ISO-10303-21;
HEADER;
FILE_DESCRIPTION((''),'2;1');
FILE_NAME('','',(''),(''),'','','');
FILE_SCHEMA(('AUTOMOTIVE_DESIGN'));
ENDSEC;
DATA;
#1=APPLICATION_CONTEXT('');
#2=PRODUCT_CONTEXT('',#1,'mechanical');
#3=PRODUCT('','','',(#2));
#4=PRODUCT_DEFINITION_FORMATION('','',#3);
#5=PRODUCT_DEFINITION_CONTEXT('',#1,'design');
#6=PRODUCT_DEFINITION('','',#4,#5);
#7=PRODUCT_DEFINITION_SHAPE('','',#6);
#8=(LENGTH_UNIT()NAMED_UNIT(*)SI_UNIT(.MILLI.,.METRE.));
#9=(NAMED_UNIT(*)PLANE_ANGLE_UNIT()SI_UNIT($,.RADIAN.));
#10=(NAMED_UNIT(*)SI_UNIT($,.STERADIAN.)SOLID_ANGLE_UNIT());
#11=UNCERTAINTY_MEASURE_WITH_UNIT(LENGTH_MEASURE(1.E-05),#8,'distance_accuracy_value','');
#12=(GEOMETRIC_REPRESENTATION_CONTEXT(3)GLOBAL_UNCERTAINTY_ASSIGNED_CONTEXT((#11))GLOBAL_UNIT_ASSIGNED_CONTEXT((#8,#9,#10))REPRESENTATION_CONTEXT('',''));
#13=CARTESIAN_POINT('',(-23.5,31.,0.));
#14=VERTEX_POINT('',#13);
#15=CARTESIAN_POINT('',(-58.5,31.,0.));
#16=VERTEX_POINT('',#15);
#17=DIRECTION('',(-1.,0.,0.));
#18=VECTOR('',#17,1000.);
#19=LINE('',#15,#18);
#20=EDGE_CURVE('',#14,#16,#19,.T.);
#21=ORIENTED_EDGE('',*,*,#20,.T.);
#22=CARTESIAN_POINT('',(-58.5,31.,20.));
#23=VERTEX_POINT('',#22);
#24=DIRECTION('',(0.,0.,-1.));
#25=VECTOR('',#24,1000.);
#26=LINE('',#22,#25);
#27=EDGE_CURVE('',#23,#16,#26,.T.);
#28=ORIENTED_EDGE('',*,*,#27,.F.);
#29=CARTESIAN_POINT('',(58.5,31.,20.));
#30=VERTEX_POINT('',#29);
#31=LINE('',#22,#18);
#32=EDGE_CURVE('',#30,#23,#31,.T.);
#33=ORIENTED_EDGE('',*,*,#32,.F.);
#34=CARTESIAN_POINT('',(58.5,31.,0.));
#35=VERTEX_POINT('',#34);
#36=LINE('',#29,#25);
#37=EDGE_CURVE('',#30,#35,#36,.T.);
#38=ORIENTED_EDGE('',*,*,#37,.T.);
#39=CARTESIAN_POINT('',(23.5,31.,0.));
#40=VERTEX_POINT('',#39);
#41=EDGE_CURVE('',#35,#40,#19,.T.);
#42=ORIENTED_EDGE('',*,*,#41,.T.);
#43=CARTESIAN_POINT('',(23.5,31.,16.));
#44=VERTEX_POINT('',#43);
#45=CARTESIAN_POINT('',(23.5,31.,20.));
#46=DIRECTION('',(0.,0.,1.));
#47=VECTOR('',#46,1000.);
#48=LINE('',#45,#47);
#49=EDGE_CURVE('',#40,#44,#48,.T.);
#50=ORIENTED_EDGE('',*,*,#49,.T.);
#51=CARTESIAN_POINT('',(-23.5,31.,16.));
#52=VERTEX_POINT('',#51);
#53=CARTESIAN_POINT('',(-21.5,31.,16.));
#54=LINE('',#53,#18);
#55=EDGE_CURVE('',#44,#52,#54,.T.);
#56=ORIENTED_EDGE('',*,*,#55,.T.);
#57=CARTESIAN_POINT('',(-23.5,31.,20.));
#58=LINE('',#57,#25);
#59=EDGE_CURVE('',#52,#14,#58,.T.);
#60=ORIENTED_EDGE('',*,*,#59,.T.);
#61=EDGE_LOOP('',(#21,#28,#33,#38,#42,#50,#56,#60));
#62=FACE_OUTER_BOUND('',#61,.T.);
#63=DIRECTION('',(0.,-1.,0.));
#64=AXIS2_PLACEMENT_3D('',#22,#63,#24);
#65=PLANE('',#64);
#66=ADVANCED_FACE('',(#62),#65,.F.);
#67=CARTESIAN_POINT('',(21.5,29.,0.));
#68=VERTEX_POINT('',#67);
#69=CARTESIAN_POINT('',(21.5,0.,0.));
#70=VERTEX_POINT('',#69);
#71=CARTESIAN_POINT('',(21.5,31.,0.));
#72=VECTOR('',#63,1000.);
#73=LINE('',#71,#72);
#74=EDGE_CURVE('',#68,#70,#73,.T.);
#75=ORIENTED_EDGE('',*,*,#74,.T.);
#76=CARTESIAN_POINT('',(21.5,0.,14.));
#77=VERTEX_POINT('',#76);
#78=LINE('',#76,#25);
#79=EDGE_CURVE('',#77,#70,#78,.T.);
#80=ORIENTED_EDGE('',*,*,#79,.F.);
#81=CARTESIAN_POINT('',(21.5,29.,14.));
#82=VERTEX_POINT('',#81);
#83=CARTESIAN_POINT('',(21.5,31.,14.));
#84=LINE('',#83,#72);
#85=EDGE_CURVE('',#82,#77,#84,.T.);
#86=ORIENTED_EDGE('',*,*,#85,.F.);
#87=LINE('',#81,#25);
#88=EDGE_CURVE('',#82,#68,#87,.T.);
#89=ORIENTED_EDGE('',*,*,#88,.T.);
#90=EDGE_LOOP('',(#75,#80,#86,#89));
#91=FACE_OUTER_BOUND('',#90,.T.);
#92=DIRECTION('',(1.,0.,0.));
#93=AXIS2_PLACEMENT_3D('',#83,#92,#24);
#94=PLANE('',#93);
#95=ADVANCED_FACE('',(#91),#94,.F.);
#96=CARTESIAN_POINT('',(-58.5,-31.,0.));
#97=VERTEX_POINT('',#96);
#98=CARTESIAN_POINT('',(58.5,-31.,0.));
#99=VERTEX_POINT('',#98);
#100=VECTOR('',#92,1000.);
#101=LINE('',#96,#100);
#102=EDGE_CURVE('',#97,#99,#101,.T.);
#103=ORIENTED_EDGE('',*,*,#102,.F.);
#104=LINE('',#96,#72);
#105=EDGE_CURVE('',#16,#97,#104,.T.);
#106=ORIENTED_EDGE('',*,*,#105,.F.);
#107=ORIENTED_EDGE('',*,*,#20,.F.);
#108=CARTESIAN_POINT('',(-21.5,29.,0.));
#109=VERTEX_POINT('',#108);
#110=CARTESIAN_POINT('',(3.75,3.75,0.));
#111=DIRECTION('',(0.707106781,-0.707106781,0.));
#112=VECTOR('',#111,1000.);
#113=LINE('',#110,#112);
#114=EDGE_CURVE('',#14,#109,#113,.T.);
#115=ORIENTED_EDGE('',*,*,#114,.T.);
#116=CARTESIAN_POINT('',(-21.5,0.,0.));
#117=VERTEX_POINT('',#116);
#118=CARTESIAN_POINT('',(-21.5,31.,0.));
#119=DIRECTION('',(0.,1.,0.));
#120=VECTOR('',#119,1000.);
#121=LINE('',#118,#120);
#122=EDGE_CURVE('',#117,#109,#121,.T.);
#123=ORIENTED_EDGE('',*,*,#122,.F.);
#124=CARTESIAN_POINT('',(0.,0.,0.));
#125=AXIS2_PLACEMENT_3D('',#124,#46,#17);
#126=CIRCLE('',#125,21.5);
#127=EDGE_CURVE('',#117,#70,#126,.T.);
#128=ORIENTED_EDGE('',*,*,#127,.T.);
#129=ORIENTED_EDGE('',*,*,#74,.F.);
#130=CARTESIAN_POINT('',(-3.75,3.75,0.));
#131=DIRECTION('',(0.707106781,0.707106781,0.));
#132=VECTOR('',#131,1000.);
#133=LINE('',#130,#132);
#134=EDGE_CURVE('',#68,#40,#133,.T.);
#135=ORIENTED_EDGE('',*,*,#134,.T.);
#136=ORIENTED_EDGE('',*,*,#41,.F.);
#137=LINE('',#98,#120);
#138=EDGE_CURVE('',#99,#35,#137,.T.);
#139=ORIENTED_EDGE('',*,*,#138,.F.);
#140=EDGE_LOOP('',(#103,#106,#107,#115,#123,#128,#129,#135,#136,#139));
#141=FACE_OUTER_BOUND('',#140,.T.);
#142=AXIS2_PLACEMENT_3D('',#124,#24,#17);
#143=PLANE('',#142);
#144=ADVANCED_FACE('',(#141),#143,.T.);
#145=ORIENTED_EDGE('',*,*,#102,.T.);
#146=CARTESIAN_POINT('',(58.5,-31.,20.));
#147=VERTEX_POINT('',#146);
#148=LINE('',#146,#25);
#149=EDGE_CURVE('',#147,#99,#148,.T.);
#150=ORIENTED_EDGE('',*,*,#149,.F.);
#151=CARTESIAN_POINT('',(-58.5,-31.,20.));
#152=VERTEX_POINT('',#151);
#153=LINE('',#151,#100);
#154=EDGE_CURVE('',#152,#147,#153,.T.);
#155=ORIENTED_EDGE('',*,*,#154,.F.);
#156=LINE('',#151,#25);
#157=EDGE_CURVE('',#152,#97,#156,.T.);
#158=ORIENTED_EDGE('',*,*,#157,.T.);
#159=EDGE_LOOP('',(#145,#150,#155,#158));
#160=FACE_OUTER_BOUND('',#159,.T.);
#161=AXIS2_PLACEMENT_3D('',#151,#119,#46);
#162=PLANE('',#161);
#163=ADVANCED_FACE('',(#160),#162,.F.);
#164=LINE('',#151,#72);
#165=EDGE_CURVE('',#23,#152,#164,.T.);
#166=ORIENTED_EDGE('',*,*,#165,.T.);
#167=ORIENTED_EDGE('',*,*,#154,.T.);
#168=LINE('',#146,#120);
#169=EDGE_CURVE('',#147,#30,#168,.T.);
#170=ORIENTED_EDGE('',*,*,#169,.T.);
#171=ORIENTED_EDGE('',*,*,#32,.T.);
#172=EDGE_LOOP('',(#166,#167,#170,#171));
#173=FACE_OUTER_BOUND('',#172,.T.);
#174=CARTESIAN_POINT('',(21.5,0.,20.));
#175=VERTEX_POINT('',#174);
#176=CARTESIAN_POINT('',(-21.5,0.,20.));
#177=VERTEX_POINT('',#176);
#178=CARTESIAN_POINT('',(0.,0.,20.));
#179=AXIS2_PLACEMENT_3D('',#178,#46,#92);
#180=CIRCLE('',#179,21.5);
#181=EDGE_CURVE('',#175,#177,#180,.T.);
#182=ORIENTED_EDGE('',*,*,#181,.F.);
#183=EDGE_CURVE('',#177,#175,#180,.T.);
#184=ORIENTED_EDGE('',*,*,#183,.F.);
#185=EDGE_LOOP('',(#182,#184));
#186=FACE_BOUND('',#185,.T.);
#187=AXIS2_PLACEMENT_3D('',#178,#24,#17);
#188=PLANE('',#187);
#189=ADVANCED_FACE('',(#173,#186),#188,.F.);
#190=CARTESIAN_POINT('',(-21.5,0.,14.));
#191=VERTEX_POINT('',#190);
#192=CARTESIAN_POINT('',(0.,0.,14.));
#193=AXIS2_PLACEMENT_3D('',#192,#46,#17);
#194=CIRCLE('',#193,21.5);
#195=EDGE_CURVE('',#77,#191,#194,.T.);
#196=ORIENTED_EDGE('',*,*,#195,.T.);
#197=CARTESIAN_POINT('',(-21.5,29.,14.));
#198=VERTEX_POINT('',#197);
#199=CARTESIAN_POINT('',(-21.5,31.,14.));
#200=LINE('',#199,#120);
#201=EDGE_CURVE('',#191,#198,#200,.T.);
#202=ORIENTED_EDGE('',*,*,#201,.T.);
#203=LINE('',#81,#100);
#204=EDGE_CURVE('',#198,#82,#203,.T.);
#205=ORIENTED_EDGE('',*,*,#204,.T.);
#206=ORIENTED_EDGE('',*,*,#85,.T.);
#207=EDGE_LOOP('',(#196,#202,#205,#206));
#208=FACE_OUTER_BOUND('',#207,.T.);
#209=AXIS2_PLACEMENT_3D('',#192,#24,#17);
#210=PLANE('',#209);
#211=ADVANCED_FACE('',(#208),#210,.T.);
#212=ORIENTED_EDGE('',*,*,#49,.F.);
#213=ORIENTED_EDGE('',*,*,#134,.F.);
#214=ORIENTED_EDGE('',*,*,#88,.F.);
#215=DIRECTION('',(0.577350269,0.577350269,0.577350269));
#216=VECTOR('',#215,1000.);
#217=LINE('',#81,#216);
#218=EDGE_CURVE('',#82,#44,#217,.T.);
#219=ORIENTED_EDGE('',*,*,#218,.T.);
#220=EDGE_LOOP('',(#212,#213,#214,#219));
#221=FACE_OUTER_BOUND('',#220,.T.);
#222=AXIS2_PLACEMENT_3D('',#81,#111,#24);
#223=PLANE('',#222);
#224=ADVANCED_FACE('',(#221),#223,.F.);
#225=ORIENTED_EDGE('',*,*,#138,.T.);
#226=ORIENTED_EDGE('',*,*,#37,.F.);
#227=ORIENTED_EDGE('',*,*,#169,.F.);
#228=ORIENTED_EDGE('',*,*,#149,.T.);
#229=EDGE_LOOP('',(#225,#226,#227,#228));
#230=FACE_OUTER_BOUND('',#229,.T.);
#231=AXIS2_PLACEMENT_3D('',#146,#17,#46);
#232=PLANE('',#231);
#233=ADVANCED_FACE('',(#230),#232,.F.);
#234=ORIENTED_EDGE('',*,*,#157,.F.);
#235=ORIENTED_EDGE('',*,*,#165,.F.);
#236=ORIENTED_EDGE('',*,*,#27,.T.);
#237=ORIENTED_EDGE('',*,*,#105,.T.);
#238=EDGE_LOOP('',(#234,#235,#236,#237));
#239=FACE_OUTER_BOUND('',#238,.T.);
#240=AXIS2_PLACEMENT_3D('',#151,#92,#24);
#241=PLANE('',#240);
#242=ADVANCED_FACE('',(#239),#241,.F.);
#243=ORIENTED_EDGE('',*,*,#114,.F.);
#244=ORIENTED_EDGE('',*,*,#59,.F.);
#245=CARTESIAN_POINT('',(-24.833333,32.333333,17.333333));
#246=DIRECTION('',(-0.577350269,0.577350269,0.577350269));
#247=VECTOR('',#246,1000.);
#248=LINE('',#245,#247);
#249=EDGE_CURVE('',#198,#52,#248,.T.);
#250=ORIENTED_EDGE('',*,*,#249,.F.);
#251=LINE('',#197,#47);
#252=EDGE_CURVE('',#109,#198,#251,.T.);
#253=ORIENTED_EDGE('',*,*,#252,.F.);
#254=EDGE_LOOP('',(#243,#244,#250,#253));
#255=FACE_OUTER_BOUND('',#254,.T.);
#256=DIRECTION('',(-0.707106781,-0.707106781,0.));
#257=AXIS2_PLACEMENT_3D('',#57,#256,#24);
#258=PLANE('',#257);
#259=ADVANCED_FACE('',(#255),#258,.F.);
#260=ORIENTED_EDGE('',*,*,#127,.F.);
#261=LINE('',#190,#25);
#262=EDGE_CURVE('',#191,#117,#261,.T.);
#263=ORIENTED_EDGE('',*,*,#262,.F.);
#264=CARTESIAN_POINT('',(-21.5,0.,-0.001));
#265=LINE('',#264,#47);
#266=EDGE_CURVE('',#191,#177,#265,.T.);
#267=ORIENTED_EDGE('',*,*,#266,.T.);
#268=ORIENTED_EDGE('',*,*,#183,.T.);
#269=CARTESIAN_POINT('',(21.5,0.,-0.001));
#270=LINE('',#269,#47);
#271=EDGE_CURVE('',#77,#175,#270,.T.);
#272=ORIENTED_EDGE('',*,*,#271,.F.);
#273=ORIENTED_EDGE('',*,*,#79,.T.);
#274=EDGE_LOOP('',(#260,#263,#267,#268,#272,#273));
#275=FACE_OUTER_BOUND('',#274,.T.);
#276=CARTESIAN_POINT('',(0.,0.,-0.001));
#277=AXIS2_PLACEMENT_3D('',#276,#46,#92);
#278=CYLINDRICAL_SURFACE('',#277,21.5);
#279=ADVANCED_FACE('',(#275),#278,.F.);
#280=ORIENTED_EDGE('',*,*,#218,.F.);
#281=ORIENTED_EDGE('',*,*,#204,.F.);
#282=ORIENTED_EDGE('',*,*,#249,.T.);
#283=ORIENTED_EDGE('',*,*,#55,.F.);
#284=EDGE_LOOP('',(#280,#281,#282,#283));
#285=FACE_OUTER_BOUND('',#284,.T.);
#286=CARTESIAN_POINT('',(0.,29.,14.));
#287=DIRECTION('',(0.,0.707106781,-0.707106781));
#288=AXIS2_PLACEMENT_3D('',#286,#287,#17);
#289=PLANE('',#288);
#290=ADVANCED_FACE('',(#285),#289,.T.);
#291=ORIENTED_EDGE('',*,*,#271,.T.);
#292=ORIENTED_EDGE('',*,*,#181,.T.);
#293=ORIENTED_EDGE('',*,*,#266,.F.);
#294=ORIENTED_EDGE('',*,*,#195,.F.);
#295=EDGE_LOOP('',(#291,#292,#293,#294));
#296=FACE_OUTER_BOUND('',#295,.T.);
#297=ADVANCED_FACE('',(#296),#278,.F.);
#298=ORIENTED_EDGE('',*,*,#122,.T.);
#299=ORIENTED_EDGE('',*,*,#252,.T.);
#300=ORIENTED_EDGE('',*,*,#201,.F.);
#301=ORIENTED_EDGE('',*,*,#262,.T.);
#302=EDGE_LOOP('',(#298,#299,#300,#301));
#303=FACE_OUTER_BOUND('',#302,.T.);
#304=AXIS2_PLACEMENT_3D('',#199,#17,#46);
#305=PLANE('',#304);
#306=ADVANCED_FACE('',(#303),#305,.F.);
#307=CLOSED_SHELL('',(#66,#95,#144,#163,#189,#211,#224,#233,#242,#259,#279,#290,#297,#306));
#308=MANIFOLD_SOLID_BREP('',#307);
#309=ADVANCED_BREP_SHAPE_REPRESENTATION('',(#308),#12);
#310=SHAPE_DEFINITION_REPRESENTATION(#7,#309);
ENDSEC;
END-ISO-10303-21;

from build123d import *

# Parameters (mm, degrees)
SKETCH_1_W          = 117
SKETCH_1_H          = 62
EXTRUDE_1_DEPTH     = 20
CUT_EXTRUDE_1_REACH = 71.161
SKETCH_2_R          = 21.5
SKETCH_3_W          = 43
SKETCH_3_H          = 31
CUT_EXTRUDE_2_DEPTH = 14
CHAMFER_1_SIZE      = 2


with BuildPart() as part:
    # 草图1 → 凸台-拉伸1 (new body)
    with BuildSketch(Plane.XY):
        Rectangle(SKETCH_1_W, SKETCH_1_H)
    extrude(amount=EXTRUDE_1_DEPTH)

    # 草图2 → 切除-拉伸1 (cut, up to next)
    with BuildSketch(Plane.XY.offset(20), mode=Mode.PRIVATE) as cut_extrude_1_sk1:
        Circle(SKETCH_2_R)
    cut_extrude_1_tool1 = extrude(cut_extrude_1_sk1.sketch, amount=-CUT_EXTRUDE_1_REACH, mode=Mode.PRIVATE) & part.part
    add(cut_extrude_1_tool1.solids().sort_by_distance((0, 0, 20))[0], mode=Mode.SUBTRACT)

    # 草图3 → 切除-拉伸2 (cut)
    with BuildSketch(Plane(origin=(0, 0, 0), x_dir=(-1, 0, 0), z_dir=(0, 0, -1))):
        with Locations((0, 15.5)):
            Rectangle(SKETCH_3_W, SKETCH_3_H)
    extrude(amount=-CUT_EXTRUDE_2_DEPTH, mode=Mode.SUBTRACT)

    # 倒角1
    chamfer_1_edges = [part.edges().sort_by_distance(p)[0] for p in [
        (0, 31, 14),
        (21.5, 31, 7),
        (-21.5, 31, 7),
    ]]
    chamfer(chamfer_1_edges, length=CHAMFER_1_SIZE)


solid = part.part
